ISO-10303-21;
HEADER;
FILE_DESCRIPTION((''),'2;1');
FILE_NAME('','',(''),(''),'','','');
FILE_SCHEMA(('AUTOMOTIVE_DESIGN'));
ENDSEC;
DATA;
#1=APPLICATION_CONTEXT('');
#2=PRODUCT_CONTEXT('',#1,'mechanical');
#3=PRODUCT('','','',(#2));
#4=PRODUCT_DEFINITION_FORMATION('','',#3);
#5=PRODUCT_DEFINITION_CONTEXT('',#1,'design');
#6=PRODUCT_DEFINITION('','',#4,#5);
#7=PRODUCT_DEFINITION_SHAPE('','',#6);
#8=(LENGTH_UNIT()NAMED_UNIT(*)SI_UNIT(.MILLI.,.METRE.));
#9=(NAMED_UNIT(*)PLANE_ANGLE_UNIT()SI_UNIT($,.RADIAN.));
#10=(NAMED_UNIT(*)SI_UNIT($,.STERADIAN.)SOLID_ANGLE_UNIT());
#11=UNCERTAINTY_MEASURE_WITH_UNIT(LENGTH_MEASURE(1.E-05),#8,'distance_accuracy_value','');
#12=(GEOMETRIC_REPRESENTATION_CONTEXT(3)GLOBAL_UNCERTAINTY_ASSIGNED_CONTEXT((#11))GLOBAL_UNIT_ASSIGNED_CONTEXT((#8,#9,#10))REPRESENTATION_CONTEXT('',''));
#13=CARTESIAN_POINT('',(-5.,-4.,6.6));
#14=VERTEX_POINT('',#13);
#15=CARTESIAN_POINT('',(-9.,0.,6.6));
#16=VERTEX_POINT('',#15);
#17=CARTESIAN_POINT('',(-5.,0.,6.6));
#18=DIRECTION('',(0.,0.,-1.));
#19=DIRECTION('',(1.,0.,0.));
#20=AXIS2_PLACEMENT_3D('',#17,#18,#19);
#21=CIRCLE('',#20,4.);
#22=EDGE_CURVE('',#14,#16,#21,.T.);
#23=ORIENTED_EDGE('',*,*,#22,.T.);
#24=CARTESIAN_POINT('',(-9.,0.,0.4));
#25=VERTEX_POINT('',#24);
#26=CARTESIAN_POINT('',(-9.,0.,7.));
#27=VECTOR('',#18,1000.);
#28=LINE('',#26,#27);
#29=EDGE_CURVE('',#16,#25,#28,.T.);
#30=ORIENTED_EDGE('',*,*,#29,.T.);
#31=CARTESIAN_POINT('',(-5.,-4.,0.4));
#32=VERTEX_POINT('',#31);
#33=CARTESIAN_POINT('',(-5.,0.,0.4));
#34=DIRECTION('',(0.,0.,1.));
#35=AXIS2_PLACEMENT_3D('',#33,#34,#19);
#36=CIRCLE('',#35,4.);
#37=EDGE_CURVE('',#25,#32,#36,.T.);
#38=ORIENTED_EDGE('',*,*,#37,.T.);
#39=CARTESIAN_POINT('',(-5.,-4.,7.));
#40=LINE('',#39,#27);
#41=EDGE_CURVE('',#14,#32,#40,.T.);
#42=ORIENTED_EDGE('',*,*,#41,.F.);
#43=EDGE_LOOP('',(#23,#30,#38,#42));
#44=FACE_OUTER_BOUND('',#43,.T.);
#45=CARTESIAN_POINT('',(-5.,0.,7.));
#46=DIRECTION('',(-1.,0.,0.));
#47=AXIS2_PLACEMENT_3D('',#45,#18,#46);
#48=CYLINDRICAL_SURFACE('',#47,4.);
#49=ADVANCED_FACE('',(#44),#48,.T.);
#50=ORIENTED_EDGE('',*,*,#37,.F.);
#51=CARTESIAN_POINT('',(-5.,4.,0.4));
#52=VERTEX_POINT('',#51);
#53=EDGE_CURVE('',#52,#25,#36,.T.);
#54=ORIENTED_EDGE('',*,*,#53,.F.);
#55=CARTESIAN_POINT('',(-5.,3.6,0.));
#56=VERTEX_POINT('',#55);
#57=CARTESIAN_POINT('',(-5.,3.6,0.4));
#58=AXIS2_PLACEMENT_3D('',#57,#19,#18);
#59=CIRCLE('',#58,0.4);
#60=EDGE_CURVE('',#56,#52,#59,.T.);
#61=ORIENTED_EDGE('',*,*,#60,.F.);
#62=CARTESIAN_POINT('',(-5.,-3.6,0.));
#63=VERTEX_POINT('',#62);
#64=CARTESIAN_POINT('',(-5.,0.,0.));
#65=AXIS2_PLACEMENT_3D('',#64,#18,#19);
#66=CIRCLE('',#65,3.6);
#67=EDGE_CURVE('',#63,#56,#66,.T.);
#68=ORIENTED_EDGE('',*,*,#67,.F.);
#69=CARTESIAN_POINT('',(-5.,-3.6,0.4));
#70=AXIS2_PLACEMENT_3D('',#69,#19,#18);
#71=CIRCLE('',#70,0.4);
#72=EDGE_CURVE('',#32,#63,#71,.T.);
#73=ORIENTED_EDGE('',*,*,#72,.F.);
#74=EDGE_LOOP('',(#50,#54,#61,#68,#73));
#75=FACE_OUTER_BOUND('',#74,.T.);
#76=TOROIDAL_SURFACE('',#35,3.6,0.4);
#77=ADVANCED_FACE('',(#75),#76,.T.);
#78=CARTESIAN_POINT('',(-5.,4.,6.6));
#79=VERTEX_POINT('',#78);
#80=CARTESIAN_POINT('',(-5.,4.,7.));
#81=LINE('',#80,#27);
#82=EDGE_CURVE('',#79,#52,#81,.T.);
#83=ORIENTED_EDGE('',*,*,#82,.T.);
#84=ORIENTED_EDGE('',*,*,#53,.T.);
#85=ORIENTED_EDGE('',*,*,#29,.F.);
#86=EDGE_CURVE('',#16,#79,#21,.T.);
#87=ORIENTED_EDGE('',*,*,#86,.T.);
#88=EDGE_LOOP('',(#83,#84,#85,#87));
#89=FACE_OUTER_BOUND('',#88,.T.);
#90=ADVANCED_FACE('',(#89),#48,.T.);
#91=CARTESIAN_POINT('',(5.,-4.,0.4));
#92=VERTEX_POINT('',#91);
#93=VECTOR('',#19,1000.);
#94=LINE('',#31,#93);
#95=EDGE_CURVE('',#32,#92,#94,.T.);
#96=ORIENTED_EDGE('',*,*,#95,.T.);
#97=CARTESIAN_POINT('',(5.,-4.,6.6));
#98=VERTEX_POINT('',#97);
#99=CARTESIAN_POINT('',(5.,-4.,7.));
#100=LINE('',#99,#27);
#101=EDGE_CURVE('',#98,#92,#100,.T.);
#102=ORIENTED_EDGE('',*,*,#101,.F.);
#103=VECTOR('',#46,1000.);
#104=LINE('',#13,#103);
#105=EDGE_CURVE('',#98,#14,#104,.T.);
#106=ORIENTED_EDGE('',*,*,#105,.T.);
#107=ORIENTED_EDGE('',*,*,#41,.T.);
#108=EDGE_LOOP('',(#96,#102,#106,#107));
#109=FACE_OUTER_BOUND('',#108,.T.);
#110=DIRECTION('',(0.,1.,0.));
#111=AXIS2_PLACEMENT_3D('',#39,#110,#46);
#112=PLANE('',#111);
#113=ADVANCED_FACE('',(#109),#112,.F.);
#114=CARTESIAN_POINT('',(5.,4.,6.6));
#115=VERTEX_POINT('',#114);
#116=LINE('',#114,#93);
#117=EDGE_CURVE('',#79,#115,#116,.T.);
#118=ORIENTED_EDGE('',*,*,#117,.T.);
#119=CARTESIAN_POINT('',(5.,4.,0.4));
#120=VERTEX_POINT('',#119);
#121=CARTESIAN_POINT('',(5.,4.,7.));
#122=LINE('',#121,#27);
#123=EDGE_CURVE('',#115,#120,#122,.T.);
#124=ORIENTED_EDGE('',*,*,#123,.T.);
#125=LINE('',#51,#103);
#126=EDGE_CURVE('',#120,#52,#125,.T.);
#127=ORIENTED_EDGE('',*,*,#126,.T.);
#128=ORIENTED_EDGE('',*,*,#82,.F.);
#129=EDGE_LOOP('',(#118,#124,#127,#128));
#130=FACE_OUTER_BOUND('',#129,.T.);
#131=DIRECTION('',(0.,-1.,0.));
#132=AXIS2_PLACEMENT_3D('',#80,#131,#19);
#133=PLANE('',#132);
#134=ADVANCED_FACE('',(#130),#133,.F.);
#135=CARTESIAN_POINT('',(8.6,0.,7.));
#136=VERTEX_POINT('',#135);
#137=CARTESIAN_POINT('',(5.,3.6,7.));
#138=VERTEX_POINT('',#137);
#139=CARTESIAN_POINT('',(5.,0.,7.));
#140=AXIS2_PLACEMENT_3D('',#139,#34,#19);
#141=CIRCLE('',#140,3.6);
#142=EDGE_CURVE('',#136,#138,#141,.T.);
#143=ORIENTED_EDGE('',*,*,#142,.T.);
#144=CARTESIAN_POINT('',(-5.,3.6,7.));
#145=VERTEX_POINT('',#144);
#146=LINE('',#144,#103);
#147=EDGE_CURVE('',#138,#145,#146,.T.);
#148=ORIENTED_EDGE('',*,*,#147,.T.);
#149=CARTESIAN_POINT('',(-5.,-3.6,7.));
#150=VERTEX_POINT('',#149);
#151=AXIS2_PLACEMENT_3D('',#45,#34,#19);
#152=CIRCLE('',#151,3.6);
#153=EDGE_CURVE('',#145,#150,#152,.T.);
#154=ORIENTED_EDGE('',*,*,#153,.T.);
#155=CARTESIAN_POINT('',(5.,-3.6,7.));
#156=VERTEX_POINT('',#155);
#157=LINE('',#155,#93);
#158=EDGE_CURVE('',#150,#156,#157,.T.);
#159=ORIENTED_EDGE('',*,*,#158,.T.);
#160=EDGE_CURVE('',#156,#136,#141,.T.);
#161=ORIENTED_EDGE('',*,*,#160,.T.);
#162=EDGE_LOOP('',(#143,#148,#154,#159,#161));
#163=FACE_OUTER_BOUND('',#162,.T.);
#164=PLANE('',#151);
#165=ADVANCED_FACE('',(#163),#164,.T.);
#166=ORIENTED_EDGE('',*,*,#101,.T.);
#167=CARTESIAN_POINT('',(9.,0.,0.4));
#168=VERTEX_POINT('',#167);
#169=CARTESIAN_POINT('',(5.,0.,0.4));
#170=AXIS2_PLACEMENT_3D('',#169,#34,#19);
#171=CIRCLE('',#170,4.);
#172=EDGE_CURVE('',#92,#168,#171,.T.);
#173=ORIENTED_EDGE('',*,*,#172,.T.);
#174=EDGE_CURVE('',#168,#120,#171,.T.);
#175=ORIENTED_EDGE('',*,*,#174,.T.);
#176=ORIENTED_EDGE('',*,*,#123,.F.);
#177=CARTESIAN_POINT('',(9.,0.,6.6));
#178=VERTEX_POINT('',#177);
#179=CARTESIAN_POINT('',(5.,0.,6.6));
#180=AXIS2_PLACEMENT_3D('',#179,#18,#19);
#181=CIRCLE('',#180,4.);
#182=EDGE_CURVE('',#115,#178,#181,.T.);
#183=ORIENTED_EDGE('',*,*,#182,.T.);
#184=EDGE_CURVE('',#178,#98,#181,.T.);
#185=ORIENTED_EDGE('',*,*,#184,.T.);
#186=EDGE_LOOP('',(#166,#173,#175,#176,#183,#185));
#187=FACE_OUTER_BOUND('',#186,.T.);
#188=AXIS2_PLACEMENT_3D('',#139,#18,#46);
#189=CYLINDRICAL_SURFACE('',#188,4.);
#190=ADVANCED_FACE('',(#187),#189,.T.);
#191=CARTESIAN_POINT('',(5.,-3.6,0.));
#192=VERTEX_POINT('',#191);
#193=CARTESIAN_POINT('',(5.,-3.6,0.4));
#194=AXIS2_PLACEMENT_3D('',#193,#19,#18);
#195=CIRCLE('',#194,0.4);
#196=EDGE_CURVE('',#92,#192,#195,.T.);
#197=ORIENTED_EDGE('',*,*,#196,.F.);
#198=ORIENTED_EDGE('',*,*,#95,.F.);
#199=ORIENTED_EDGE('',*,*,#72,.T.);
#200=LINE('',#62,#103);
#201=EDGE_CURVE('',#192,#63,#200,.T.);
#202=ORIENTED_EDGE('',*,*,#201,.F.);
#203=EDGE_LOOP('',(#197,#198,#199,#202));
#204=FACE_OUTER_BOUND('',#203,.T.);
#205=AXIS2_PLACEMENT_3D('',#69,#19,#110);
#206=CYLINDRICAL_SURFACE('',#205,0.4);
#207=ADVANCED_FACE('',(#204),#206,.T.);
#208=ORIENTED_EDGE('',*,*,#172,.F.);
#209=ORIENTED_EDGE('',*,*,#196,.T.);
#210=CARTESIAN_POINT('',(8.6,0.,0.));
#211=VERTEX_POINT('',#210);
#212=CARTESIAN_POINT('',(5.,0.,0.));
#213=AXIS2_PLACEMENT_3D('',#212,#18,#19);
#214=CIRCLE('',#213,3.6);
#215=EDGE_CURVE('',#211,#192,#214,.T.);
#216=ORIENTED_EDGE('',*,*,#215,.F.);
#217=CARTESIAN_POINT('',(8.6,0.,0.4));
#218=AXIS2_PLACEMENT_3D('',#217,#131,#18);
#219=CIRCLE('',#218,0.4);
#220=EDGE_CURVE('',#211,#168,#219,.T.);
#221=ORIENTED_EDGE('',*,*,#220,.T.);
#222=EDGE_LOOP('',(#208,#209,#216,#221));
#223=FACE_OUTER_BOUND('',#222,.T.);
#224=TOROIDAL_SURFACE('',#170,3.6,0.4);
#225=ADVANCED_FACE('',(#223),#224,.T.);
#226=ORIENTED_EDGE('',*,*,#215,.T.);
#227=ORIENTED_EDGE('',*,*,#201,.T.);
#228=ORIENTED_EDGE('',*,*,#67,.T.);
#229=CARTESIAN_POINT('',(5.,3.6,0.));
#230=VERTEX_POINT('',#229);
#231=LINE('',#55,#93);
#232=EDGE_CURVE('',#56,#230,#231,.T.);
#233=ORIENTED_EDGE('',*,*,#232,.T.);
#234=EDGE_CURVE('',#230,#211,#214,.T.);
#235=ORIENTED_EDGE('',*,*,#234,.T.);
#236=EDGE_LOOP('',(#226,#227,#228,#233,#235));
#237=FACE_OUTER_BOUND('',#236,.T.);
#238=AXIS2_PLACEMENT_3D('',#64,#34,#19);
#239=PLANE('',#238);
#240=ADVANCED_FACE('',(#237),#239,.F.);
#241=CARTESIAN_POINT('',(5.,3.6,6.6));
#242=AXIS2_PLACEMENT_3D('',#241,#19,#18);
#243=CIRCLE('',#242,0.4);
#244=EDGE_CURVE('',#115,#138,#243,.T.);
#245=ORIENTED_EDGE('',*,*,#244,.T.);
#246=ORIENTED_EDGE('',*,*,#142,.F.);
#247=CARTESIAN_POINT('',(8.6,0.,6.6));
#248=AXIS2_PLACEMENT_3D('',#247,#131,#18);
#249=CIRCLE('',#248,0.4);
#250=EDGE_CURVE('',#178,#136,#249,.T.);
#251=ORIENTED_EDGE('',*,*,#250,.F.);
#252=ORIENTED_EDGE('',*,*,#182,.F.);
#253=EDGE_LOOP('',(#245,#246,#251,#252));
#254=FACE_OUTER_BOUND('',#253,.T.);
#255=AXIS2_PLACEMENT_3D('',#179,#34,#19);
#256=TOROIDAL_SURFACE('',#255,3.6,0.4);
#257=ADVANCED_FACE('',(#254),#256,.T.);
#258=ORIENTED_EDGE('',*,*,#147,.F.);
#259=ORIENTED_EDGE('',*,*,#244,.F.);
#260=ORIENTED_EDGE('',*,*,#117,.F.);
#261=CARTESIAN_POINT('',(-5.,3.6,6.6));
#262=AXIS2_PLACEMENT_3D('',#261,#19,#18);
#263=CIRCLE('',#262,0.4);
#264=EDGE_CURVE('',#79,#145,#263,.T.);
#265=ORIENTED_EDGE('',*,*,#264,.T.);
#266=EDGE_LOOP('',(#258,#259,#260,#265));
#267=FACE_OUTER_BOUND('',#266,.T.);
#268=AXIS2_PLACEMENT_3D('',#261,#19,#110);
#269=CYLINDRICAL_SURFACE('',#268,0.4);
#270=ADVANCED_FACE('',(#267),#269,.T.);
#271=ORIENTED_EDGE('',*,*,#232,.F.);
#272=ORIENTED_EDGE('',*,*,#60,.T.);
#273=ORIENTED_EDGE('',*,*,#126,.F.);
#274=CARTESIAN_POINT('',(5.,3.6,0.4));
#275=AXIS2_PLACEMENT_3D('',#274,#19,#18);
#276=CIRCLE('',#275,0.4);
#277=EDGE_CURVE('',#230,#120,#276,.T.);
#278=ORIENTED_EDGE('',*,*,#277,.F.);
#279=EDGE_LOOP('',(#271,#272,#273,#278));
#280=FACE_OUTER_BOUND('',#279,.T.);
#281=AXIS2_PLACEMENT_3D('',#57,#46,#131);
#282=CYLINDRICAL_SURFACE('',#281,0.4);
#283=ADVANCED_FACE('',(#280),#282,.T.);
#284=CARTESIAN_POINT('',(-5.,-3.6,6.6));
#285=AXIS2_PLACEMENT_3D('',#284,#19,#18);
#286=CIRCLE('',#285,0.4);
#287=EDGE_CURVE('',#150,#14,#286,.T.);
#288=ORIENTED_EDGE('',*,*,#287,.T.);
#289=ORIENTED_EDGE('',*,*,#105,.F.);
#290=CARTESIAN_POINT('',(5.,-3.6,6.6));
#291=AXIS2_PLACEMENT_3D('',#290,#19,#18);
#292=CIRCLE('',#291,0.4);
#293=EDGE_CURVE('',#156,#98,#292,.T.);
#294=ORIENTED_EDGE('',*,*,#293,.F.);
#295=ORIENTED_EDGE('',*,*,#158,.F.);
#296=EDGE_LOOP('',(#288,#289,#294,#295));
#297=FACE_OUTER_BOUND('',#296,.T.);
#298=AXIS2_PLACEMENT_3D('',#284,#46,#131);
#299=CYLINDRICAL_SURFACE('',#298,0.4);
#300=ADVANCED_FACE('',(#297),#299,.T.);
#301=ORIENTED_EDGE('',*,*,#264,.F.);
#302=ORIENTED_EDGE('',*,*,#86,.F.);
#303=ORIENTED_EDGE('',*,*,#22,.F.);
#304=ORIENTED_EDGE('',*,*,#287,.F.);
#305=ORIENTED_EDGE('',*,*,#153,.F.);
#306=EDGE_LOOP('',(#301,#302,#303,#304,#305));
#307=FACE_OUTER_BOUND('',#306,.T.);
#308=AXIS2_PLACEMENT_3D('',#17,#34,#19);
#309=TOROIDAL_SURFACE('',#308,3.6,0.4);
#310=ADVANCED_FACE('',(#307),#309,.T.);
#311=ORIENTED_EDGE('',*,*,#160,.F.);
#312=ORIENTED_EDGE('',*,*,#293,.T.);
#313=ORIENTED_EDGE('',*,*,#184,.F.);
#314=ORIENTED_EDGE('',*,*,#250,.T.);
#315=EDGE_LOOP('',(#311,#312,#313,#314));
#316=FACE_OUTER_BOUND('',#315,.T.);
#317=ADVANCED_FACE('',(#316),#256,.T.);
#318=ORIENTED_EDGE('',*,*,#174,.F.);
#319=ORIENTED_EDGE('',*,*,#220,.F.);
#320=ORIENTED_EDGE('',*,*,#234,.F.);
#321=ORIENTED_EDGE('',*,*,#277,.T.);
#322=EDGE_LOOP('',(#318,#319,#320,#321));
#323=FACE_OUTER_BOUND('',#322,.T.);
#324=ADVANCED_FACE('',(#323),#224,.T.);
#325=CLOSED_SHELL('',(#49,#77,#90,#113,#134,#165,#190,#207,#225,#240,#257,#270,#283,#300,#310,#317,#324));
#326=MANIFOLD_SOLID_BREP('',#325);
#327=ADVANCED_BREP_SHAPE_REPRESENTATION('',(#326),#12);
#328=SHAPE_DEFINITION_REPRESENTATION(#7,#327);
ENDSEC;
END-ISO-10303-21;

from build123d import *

# Parameters (mm, degrees)
EXTRUDE_523_DEPTH = 7
FILLET_1_R        = 0.4


with BuildPart() as part:
    # 草图1 → Extrude 523 (new body)
    with BuildSketch(Plane.XY):
        with BuildLine():
            Line((-5, 4), (5, 4))
            ThreePointArc((5, 4), (9, 0), (5, -4))
            Line((5, -4), (-5, -4))
            ThreePointArc((-5, -4), (-9, 0), (-5, 4))
        make_face()
    extrude(amount=EXTRUDE_523_DEPTH)

    # 圆角1
    fillet_1_edges = [part.edges().sort_by_distance(p)[0] for p in [
        (9, 0, 7),
        (0, 4, 7),
        (-9, 0, 7),
        (0, 4, 0),
        (9, 0, 0),
        (0, -4, 0),
        (-9, 0, 0),
        (0, -4, 7),
    ]]
    fillet(fillet_1_edges, radius=FILLET_1_R)


solid = part.part
